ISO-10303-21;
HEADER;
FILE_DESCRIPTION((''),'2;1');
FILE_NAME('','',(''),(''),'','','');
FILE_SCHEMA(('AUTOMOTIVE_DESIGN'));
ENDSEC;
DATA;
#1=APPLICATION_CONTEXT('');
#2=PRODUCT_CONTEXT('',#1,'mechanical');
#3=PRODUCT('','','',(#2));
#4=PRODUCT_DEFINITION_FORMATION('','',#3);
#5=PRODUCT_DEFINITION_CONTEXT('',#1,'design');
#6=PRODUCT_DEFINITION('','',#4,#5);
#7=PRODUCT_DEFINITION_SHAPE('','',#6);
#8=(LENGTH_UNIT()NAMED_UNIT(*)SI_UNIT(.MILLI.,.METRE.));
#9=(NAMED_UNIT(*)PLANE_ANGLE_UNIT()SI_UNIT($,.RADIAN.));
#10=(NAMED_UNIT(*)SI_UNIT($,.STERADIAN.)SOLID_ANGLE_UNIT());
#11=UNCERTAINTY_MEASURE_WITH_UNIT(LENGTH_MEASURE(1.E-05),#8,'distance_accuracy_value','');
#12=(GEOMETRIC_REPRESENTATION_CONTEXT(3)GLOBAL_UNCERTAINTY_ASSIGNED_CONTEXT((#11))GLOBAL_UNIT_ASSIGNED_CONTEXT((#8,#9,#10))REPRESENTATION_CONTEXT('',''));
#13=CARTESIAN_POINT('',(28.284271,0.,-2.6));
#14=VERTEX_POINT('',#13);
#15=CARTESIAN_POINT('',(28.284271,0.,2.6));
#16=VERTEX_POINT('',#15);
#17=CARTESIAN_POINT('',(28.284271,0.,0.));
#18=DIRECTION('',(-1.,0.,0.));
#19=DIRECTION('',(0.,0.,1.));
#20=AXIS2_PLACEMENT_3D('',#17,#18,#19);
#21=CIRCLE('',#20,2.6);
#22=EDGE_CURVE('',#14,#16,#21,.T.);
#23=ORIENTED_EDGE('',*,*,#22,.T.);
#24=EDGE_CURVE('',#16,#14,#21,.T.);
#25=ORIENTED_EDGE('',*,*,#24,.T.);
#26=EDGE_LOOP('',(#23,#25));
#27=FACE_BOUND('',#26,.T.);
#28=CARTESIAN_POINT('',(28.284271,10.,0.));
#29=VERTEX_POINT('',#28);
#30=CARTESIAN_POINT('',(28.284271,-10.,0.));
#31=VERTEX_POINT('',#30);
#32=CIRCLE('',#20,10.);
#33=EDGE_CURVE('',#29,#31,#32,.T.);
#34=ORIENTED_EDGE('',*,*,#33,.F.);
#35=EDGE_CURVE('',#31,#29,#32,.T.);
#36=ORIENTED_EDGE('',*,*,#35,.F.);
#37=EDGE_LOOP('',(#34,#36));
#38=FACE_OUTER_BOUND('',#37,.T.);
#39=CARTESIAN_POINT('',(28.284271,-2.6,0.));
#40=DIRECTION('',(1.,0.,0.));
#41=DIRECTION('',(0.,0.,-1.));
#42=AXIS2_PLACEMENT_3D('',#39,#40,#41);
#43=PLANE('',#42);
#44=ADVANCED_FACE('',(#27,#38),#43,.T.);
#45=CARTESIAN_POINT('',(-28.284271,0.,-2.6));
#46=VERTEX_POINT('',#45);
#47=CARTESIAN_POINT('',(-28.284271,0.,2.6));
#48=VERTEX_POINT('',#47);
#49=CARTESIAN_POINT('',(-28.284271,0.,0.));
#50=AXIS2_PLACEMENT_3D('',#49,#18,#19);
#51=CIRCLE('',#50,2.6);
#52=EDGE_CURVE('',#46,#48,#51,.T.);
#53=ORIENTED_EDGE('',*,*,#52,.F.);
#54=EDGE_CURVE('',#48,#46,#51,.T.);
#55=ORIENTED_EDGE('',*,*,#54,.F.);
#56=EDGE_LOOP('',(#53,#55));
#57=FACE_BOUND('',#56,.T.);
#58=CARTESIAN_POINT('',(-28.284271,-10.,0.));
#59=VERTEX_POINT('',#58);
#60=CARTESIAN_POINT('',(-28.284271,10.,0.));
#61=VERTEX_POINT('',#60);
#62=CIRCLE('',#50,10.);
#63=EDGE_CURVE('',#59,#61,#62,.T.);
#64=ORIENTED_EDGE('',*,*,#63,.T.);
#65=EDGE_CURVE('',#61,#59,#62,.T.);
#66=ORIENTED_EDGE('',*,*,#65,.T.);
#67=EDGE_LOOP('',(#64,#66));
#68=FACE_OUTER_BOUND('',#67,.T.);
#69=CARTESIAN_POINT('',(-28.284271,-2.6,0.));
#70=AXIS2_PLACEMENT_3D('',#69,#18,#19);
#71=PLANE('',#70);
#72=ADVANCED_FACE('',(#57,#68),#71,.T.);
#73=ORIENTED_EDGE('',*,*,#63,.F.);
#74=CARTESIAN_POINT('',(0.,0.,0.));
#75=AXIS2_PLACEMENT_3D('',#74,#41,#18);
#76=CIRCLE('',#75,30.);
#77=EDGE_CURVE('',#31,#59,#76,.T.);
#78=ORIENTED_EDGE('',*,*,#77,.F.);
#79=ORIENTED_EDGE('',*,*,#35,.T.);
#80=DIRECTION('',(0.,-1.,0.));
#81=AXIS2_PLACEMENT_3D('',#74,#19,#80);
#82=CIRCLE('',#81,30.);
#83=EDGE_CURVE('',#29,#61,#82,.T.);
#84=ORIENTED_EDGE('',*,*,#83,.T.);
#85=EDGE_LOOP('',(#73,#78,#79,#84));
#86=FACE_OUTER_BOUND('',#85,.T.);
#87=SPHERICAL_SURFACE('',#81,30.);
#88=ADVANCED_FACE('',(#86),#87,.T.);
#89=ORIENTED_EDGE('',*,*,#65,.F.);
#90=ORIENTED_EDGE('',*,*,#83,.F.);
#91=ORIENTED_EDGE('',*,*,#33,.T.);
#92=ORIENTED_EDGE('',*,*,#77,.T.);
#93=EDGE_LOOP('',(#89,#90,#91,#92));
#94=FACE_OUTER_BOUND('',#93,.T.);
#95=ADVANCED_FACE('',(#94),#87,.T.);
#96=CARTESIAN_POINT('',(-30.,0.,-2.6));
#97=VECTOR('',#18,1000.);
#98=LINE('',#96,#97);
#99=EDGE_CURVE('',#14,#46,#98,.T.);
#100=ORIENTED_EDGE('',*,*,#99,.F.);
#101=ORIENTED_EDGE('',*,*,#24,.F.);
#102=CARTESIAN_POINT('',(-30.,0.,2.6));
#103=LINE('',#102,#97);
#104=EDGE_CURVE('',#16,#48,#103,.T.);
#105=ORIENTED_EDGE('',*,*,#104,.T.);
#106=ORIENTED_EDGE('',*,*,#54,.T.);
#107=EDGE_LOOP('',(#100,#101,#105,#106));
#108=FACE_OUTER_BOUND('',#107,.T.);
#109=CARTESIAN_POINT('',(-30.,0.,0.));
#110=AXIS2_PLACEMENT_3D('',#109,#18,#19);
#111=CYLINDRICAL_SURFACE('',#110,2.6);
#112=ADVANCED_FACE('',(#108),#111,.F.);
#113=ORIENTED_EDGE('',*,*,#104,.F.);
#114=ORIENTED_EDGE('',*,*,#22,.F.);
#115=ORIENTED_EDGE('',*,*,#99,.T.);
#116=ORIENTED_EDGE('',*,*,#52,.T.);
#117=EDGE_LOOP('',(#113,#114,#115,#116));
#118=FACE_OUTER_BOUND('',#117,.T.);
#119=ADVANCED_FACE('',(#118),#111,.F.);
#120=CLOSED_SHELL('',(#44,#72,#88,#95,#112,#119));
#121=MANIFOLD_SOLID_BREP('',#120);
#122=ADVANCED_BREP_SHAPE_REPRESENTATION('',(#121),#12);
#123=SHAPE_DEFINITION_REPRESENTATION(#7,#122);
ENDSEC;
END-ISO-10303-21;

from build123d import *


with BuildPart() as part:
    # Knob Profile Sketch → Ball Knob Revolve (revolve)
    with BuildSketch(Plane.XY, mode=Mode.PRIVATE) as ball_knob_revolve_sk:
        with BuildLine():
            Line((-28.284271247, -2.6), (-28.284271247, -10))
            ThreePointArc((-28.284271247, -10), (0, -30), (28.284271247, -10))
            Line((28.284271247, -10), (28.284271247, -2.6))
            Line((28.284271247, -2.6), (-28.284271247, -2.6))
        make_face()
    revolve(ball_knob_revolve_sk.sketch.rotate(Axis((-30, 0, 0), (1, 0, 0)), 270), axis=Axis((-30, 0, 0), (1, 0, 0)))


solid = part.part
